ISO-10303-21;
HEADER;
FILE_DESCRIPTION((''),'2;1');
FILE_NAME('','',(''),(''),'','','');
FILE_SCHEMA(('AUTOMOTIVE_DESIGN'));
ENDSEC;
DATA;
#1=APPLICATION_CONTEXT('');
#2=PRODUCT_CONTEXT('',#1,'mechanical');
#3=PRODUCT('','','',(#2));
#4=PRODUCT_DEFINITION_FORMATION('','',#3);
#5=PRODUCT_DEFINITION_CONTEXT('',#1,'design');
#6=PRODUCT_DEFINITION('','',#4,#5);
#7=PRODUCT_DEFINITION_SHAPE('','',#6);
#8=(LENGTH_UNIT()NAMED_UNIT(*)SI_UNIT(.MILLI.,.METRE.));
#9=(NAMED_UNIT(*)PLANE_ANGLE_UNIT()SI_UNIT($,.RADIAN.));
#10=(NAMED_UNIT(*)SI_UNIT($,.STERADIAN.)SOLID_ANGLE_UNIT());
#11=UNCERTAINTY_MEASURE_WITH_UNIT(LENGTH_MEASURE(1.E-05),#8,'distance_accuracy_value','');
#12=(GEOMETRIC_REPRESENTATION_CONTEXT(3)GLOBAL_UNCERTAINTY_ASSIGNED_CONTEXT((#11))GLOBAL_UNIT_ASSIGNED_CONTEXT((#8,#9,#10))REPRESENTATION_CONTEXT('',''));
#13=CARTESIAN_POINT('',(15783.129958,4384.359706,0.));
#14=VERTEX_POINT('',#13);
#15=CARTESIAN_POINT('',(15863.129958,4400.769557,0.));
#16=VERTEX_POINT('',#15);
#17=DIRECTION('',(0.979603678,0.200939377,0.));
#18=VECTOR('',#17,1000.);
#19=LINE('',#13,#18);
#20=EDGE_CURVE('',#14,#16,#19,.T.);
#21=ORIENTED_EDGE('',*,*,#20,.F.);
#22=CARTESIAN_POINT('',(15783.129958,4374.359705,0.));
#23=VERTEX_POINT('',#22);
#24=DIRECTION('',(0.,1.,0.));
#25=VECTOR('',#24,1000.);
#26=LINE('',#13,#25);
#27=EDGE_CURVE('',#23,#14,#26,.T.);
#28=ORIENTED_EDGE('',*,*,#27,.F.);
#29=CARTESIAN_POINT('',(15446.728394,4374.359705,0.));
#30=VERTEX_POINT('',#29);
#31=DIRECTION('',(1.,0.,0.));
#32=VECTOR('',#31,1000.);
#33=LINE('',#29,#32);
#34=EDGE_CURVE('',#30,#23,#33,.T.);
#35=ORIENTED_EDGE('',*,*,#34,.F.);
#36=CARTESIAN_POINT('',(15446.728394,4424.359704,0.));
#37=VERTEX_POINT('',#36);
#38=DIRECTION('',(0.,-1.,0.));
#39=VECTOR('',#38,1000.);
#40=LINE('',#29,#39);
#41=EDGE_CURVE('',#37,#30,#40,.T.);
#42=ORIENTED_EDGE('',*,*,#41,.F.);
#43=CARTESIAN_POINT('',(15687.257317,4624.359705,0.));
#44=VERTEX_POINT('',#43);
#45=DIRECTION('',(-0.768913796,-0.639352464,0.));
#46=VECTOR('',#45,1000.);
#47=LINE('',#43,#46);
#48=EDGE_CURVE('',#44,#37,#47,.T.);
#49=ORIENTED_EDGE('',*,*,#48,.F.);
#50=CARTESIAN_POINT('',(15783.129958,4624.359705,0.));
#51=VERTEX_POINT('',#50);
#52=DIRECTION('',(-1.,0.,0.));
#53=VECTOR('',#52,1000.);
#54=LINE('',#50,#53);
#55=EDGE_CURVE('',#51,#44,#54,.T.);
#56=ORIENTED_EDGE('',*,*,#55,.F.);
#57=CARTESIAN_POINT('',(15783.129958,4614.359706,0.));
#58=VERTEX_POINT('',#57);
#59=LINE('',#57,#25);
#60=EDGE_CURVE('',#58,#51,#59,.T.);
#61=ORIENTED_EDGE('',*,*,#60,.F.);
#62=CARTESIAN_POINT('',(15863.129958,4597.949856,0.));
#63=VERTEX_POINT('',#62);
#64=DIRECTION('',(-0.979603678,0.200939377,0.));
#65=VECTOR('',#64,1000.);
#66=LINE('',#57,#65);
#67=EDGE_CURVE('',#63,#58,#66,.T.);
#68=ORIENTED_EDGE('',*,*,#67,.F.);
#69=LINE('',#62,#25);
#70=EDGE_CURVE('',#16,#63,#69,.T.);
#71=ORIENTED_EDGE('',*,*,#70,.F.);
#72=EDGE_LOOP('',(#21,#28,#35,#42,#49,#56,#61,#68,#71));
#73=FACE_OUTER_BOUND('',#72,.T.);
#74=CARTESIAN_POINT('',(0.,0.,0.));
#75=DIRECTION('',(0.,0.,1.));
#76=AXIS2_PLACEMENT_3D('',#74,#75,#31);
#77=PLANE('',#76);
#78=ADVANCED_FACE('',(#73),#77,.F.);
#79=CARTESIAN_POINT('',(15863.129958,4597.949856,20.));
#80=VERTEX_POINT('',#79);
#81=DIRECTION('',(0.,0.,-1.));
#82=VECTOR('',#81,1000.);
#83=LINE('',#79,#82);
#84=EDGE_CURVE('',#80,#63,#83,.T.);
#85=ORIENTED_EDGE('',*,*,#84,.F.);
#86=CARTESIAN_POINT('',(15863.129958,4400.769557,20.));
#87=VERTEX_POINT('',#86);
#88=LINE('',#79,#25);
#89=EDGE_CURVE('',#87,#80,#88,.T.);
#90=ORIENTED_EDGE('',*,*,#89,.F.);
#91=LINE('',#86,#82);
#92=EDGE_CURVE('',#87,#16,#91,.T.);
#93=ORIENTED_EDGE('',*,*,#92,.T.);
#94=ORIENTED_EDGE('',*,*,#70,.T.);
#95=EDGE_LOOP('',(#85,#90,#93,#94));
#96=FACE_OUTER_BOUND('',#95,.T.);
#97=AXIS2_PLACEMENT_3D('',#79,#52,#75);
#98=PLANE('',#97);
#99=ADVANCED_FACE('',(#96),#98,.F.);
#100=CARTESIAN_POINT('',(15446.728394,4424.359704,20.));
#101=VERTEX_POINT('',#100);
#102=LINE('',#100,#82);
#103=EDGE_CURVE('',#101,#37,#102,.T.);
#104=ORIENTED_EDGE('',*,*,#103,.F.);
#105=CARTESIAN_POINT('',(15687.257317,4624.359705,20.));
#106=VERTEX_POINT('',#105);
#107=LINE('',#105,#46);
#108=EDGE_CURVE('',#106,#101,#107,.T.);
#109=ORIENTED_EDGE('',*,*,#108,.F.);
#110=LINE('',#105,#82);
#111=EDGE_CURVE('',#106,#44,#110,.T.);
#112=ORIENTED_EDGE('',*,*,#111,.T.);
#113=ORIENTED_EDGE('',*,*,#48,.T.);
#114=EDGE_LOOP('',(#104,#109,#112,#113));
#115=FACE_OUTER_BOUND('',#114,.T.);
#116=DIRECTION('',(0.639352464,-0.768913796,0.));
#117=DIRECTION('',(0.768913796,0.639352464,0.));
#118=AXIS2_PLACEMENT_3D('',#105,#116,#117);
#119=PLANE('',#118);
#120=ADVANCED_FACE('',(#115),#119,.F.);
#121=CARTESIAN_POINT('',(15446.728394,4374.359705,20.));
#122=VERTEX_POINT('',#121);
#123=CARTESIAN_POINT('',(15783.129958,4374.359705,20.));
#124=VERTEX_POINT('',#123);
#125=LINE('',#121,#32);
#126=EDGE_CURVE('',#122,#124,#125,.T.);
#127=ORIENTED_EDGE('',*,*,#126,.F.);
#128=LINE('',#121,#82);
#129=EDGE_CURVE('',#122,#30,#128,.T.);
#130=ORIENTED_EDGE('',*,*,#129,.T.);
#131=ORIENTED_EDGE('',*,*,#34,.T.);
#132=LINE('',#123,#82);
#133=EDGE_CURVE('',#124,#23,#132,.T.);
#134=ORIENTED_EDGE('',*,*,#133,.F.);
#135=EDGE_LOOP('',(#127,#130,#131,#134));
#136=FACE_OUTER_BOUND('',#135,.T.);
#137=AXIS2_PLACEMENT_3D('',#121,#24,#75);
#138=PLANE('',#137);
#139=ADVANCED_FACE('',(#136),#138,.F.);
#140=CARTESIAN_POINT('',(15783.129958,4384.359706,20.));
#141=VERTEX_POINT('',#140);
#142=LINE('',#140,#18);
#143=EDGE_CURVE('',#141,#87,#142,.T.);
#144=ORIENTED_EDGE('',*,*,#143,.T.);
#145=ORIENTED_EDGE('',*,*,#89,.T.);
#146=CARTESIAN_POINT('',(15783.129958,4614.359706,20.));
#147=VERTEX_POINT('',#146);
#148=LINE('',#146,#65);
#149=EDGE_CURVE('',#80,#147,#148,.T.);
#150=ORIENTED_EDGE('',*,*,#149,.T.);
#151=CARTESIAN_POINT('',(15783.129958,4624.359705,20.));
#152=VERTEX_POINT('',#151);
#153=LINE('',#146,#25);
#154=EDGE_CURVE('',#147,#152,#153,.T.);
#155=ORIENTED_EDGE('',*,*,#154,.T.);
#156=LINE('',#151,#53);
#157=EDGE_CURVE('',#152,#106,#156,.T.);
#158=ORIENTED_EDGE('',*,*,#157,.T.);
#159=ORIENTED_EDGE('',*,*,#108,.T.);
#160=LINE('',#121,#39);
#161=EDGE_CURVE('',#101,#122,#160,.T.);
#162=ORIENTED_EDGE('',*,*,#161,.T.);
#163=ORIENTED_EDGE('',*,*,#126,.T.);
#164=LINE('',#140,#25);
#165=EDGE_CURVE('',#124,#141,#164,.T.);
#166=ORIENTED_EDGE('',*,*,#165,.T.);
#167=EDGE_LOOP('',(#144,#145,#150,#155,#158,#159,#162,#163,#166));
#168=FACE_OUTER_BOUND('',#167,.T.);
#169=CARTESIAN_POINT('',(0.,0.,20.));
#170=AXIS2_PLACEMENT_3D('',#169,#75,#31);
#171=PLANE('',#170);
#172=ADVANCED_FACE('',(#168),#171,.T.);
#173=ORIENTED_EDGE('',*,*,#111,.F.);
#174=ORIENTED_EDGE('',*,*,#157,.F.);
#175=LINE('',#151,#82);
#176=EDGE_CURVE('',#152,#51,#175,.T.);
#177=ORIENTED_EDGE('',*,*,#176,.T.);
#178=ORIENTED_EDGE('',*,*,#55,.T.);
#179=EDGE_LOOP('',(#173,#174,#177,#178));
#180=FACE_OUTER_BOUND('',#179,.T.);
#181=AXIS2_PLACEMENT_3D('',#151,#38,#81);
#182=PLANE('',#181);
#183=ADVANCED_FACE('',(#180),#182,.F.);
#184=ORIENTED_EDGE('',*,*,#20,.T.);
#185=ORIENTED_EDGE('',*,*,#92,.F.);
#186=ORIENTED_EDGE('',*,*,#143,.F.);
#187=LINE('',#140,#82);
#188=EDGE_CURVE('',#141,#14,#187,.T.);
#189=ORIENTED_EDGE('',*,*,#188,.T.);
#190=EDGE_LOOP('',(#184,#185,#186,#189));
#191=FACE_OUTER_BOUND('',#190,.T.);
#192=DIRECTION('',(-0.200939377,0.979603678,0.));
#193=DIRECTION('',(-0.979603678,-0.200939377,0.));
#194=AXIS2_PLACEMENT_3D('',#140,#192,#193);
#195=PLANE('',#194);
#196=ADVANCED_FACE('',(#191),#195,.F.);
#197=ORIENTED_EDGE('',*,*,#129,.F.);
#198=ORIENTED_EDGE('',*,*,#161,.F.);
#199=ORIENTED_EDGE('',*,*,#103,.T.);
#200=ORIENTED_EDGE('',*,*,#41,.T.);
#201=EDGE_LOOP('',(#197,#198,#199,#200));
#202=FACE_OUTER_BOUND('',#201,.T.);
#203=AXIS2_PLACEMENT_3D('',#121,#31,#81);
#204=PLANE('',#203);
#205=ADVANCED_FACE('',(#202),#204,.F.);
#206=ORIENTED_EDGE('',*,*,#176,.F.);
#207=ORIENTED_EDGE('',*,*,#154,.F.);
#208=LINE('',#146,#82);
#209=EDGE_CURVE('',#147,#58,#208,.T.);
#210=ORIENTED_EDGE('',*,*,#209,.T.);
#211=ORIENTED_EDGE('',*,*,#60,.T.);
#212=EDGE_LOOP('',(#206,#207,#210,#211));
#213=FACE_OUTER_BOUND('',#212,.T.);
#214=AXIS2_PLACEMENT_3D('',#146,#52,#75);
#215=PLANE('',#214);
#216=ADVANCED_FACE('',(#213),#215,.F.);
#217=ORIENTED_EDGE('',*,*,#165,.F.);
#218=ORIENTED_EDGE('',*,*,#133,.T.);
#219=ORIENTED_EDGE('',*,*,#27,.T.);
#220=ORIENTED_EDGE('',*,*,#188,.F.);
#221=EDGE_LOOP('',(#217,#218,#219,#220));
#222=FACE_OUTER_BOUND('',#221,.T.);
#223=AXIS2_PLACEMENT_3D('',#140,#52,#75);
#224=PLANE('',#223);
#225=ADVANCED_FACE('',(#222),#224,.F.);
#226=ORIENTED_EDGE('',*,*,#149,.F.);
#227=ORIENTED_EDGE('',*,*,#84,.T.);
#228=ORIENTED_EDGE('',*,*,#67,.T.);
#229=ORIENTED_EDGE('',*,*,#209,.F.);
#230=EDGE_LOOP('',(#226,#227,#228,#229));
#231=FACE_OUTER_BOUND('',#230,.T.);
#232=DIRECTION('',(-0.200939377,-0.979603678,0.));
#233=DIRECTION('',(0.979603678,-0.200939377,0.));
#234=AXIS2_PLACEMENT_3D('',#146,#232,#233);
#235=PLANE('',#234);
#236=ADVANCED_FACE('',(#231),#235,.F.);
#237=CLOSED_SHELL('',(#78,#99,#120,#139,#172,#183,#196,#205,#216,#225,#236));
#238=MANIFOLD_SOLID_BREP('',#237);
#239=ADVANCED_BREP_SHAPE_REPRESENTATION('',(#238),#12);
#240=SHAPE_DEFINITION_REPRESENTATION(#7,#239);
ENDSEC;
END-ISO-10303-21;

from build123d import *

# Parameters (mm, degrees)
BOSS_EXTRUDE1_DEPTH = 20


with BuildPart() as part:
    # Sketch1 → Boss-Extrude1 (new body)
    with BuildSketch(Plane.XY):
        Polygon((15783.129958129, 4624.359704887), (15687.257317346, 4624.359704887), (15446.728394371, 4424.359704449), (15446.728394371, 4374.359704887), (15783.129958129, 4374.359704887), (15783.129958129, 4384.359705726), (15863.129958392, 4400.769556521), (15863.129958392, 4597.949855679), (15783.129958129, 4614.359706473), align=None)
    extrude(amount=BOSS_EXTRUDE1_DEPTH)


solid = part.part
